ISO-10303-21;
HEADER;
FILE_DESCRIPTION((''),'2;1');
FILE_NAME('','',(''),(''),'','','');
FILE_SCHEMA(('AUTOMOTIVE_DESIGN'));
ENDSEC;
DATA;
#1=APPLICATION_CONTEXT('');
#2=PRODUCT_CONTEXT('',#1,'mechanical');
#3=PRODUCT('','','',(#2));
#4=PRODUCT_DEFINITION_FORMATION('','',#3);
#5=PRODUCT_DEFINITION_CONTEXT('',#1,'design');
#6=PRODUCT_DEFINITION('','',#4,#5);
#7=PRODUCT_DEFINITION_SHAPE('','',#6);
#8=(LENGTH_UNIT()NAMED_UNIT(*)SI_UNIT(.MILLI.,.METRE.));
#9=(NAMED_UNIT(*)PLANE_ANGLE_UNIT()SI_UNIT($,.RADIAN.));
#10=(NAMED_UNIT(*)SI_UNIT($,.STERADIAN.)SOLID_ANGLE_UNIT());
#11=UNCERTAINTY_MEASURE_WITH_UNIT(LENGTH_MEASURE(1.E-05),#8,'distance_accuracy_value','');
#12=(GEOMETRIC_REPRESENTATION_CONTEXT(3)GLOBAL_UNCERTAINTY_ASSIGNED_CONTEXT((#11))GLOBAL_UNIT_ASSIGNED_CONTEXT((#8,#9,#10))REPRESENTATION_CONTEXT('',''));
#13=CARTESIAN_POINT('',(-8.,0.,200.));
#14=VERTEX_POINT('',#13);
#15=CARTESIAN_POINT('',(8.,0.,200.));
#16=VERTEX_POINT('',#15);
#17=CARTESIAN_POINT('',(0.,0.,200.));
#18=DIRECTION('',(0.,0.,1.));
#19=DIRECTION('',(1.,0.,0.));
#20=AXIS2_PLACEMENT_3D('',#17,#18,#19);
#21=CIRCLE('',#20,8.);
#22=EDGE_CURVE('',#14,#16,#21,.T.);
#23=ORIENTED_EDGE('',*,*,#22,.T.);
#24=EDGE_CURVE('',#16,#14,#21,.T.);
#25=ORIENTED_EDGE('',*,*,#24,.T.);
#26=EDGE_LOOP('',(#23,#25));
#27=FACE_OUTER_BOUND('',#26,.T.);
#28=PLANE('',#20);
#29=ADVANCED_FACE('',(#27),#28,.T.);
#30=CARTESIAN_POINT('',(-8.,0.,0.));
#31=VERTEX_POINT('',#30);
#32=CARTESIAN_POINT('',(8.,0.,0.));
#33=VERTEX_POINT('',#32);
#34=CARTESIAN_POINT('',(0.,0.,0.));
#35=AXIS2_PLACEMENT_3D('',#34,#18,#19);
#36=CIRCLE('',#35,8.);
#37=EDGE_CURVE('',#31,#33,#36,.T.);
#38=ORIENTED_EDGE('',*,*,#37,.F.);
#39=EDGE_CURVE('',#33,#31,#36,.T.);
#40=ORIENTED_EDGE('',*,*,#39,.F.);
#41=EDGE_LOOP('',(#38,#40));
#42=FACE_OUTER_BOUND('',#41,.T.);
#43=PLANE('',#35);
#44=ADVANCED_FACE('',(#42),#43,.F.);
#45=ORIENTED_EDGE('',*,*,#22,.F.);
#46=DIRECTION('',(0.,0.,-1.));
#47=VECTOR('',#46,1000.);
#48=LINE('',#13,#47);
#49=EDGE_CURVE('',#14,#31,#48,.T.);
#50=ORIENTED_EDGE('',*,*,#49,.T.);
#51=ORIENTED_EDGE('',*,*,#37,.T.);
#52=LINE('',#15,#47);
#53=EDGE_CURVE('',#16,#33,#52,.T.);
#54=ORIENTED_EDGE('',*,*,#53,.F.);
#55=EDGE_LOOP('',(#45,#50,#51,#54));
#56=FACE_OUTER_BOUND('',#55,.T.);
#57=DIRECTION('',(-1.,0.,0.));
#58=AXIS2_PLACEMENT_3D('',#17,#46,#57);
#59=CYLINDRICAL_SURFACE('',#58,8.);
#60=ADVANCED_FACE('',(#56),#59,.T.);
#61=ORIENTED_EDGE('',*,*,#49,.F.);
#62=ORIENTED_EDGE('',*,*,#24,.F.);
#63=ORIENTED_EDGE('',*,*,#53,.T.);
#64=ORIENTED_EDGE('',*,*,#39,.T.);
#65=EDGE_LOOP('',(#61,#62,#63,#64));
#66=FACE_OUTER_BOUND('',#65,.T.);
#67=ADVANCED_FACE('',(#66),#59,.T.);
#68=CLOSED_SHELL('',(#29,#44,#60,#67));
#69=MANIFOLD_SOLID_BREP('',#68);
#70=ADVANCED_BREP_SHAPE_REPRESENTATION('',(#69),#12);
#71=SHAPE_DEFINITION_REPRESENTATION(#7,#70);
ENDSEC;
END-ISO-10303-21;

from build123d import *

# Parameters (mm, degrees)
SKETCH1_R           = 8
BOSS_EXTRUDE1_DEPTH = 200


with BuildPart() as part:
    # Sketch1 → Boss-Extrude1 (new body)
    with BuildSketch(Plane.XY):
        Circle(SKETCH1_R)
    extrude(amount=BOSS_EXTRUDE1_DEPTH)


solid = part.part
